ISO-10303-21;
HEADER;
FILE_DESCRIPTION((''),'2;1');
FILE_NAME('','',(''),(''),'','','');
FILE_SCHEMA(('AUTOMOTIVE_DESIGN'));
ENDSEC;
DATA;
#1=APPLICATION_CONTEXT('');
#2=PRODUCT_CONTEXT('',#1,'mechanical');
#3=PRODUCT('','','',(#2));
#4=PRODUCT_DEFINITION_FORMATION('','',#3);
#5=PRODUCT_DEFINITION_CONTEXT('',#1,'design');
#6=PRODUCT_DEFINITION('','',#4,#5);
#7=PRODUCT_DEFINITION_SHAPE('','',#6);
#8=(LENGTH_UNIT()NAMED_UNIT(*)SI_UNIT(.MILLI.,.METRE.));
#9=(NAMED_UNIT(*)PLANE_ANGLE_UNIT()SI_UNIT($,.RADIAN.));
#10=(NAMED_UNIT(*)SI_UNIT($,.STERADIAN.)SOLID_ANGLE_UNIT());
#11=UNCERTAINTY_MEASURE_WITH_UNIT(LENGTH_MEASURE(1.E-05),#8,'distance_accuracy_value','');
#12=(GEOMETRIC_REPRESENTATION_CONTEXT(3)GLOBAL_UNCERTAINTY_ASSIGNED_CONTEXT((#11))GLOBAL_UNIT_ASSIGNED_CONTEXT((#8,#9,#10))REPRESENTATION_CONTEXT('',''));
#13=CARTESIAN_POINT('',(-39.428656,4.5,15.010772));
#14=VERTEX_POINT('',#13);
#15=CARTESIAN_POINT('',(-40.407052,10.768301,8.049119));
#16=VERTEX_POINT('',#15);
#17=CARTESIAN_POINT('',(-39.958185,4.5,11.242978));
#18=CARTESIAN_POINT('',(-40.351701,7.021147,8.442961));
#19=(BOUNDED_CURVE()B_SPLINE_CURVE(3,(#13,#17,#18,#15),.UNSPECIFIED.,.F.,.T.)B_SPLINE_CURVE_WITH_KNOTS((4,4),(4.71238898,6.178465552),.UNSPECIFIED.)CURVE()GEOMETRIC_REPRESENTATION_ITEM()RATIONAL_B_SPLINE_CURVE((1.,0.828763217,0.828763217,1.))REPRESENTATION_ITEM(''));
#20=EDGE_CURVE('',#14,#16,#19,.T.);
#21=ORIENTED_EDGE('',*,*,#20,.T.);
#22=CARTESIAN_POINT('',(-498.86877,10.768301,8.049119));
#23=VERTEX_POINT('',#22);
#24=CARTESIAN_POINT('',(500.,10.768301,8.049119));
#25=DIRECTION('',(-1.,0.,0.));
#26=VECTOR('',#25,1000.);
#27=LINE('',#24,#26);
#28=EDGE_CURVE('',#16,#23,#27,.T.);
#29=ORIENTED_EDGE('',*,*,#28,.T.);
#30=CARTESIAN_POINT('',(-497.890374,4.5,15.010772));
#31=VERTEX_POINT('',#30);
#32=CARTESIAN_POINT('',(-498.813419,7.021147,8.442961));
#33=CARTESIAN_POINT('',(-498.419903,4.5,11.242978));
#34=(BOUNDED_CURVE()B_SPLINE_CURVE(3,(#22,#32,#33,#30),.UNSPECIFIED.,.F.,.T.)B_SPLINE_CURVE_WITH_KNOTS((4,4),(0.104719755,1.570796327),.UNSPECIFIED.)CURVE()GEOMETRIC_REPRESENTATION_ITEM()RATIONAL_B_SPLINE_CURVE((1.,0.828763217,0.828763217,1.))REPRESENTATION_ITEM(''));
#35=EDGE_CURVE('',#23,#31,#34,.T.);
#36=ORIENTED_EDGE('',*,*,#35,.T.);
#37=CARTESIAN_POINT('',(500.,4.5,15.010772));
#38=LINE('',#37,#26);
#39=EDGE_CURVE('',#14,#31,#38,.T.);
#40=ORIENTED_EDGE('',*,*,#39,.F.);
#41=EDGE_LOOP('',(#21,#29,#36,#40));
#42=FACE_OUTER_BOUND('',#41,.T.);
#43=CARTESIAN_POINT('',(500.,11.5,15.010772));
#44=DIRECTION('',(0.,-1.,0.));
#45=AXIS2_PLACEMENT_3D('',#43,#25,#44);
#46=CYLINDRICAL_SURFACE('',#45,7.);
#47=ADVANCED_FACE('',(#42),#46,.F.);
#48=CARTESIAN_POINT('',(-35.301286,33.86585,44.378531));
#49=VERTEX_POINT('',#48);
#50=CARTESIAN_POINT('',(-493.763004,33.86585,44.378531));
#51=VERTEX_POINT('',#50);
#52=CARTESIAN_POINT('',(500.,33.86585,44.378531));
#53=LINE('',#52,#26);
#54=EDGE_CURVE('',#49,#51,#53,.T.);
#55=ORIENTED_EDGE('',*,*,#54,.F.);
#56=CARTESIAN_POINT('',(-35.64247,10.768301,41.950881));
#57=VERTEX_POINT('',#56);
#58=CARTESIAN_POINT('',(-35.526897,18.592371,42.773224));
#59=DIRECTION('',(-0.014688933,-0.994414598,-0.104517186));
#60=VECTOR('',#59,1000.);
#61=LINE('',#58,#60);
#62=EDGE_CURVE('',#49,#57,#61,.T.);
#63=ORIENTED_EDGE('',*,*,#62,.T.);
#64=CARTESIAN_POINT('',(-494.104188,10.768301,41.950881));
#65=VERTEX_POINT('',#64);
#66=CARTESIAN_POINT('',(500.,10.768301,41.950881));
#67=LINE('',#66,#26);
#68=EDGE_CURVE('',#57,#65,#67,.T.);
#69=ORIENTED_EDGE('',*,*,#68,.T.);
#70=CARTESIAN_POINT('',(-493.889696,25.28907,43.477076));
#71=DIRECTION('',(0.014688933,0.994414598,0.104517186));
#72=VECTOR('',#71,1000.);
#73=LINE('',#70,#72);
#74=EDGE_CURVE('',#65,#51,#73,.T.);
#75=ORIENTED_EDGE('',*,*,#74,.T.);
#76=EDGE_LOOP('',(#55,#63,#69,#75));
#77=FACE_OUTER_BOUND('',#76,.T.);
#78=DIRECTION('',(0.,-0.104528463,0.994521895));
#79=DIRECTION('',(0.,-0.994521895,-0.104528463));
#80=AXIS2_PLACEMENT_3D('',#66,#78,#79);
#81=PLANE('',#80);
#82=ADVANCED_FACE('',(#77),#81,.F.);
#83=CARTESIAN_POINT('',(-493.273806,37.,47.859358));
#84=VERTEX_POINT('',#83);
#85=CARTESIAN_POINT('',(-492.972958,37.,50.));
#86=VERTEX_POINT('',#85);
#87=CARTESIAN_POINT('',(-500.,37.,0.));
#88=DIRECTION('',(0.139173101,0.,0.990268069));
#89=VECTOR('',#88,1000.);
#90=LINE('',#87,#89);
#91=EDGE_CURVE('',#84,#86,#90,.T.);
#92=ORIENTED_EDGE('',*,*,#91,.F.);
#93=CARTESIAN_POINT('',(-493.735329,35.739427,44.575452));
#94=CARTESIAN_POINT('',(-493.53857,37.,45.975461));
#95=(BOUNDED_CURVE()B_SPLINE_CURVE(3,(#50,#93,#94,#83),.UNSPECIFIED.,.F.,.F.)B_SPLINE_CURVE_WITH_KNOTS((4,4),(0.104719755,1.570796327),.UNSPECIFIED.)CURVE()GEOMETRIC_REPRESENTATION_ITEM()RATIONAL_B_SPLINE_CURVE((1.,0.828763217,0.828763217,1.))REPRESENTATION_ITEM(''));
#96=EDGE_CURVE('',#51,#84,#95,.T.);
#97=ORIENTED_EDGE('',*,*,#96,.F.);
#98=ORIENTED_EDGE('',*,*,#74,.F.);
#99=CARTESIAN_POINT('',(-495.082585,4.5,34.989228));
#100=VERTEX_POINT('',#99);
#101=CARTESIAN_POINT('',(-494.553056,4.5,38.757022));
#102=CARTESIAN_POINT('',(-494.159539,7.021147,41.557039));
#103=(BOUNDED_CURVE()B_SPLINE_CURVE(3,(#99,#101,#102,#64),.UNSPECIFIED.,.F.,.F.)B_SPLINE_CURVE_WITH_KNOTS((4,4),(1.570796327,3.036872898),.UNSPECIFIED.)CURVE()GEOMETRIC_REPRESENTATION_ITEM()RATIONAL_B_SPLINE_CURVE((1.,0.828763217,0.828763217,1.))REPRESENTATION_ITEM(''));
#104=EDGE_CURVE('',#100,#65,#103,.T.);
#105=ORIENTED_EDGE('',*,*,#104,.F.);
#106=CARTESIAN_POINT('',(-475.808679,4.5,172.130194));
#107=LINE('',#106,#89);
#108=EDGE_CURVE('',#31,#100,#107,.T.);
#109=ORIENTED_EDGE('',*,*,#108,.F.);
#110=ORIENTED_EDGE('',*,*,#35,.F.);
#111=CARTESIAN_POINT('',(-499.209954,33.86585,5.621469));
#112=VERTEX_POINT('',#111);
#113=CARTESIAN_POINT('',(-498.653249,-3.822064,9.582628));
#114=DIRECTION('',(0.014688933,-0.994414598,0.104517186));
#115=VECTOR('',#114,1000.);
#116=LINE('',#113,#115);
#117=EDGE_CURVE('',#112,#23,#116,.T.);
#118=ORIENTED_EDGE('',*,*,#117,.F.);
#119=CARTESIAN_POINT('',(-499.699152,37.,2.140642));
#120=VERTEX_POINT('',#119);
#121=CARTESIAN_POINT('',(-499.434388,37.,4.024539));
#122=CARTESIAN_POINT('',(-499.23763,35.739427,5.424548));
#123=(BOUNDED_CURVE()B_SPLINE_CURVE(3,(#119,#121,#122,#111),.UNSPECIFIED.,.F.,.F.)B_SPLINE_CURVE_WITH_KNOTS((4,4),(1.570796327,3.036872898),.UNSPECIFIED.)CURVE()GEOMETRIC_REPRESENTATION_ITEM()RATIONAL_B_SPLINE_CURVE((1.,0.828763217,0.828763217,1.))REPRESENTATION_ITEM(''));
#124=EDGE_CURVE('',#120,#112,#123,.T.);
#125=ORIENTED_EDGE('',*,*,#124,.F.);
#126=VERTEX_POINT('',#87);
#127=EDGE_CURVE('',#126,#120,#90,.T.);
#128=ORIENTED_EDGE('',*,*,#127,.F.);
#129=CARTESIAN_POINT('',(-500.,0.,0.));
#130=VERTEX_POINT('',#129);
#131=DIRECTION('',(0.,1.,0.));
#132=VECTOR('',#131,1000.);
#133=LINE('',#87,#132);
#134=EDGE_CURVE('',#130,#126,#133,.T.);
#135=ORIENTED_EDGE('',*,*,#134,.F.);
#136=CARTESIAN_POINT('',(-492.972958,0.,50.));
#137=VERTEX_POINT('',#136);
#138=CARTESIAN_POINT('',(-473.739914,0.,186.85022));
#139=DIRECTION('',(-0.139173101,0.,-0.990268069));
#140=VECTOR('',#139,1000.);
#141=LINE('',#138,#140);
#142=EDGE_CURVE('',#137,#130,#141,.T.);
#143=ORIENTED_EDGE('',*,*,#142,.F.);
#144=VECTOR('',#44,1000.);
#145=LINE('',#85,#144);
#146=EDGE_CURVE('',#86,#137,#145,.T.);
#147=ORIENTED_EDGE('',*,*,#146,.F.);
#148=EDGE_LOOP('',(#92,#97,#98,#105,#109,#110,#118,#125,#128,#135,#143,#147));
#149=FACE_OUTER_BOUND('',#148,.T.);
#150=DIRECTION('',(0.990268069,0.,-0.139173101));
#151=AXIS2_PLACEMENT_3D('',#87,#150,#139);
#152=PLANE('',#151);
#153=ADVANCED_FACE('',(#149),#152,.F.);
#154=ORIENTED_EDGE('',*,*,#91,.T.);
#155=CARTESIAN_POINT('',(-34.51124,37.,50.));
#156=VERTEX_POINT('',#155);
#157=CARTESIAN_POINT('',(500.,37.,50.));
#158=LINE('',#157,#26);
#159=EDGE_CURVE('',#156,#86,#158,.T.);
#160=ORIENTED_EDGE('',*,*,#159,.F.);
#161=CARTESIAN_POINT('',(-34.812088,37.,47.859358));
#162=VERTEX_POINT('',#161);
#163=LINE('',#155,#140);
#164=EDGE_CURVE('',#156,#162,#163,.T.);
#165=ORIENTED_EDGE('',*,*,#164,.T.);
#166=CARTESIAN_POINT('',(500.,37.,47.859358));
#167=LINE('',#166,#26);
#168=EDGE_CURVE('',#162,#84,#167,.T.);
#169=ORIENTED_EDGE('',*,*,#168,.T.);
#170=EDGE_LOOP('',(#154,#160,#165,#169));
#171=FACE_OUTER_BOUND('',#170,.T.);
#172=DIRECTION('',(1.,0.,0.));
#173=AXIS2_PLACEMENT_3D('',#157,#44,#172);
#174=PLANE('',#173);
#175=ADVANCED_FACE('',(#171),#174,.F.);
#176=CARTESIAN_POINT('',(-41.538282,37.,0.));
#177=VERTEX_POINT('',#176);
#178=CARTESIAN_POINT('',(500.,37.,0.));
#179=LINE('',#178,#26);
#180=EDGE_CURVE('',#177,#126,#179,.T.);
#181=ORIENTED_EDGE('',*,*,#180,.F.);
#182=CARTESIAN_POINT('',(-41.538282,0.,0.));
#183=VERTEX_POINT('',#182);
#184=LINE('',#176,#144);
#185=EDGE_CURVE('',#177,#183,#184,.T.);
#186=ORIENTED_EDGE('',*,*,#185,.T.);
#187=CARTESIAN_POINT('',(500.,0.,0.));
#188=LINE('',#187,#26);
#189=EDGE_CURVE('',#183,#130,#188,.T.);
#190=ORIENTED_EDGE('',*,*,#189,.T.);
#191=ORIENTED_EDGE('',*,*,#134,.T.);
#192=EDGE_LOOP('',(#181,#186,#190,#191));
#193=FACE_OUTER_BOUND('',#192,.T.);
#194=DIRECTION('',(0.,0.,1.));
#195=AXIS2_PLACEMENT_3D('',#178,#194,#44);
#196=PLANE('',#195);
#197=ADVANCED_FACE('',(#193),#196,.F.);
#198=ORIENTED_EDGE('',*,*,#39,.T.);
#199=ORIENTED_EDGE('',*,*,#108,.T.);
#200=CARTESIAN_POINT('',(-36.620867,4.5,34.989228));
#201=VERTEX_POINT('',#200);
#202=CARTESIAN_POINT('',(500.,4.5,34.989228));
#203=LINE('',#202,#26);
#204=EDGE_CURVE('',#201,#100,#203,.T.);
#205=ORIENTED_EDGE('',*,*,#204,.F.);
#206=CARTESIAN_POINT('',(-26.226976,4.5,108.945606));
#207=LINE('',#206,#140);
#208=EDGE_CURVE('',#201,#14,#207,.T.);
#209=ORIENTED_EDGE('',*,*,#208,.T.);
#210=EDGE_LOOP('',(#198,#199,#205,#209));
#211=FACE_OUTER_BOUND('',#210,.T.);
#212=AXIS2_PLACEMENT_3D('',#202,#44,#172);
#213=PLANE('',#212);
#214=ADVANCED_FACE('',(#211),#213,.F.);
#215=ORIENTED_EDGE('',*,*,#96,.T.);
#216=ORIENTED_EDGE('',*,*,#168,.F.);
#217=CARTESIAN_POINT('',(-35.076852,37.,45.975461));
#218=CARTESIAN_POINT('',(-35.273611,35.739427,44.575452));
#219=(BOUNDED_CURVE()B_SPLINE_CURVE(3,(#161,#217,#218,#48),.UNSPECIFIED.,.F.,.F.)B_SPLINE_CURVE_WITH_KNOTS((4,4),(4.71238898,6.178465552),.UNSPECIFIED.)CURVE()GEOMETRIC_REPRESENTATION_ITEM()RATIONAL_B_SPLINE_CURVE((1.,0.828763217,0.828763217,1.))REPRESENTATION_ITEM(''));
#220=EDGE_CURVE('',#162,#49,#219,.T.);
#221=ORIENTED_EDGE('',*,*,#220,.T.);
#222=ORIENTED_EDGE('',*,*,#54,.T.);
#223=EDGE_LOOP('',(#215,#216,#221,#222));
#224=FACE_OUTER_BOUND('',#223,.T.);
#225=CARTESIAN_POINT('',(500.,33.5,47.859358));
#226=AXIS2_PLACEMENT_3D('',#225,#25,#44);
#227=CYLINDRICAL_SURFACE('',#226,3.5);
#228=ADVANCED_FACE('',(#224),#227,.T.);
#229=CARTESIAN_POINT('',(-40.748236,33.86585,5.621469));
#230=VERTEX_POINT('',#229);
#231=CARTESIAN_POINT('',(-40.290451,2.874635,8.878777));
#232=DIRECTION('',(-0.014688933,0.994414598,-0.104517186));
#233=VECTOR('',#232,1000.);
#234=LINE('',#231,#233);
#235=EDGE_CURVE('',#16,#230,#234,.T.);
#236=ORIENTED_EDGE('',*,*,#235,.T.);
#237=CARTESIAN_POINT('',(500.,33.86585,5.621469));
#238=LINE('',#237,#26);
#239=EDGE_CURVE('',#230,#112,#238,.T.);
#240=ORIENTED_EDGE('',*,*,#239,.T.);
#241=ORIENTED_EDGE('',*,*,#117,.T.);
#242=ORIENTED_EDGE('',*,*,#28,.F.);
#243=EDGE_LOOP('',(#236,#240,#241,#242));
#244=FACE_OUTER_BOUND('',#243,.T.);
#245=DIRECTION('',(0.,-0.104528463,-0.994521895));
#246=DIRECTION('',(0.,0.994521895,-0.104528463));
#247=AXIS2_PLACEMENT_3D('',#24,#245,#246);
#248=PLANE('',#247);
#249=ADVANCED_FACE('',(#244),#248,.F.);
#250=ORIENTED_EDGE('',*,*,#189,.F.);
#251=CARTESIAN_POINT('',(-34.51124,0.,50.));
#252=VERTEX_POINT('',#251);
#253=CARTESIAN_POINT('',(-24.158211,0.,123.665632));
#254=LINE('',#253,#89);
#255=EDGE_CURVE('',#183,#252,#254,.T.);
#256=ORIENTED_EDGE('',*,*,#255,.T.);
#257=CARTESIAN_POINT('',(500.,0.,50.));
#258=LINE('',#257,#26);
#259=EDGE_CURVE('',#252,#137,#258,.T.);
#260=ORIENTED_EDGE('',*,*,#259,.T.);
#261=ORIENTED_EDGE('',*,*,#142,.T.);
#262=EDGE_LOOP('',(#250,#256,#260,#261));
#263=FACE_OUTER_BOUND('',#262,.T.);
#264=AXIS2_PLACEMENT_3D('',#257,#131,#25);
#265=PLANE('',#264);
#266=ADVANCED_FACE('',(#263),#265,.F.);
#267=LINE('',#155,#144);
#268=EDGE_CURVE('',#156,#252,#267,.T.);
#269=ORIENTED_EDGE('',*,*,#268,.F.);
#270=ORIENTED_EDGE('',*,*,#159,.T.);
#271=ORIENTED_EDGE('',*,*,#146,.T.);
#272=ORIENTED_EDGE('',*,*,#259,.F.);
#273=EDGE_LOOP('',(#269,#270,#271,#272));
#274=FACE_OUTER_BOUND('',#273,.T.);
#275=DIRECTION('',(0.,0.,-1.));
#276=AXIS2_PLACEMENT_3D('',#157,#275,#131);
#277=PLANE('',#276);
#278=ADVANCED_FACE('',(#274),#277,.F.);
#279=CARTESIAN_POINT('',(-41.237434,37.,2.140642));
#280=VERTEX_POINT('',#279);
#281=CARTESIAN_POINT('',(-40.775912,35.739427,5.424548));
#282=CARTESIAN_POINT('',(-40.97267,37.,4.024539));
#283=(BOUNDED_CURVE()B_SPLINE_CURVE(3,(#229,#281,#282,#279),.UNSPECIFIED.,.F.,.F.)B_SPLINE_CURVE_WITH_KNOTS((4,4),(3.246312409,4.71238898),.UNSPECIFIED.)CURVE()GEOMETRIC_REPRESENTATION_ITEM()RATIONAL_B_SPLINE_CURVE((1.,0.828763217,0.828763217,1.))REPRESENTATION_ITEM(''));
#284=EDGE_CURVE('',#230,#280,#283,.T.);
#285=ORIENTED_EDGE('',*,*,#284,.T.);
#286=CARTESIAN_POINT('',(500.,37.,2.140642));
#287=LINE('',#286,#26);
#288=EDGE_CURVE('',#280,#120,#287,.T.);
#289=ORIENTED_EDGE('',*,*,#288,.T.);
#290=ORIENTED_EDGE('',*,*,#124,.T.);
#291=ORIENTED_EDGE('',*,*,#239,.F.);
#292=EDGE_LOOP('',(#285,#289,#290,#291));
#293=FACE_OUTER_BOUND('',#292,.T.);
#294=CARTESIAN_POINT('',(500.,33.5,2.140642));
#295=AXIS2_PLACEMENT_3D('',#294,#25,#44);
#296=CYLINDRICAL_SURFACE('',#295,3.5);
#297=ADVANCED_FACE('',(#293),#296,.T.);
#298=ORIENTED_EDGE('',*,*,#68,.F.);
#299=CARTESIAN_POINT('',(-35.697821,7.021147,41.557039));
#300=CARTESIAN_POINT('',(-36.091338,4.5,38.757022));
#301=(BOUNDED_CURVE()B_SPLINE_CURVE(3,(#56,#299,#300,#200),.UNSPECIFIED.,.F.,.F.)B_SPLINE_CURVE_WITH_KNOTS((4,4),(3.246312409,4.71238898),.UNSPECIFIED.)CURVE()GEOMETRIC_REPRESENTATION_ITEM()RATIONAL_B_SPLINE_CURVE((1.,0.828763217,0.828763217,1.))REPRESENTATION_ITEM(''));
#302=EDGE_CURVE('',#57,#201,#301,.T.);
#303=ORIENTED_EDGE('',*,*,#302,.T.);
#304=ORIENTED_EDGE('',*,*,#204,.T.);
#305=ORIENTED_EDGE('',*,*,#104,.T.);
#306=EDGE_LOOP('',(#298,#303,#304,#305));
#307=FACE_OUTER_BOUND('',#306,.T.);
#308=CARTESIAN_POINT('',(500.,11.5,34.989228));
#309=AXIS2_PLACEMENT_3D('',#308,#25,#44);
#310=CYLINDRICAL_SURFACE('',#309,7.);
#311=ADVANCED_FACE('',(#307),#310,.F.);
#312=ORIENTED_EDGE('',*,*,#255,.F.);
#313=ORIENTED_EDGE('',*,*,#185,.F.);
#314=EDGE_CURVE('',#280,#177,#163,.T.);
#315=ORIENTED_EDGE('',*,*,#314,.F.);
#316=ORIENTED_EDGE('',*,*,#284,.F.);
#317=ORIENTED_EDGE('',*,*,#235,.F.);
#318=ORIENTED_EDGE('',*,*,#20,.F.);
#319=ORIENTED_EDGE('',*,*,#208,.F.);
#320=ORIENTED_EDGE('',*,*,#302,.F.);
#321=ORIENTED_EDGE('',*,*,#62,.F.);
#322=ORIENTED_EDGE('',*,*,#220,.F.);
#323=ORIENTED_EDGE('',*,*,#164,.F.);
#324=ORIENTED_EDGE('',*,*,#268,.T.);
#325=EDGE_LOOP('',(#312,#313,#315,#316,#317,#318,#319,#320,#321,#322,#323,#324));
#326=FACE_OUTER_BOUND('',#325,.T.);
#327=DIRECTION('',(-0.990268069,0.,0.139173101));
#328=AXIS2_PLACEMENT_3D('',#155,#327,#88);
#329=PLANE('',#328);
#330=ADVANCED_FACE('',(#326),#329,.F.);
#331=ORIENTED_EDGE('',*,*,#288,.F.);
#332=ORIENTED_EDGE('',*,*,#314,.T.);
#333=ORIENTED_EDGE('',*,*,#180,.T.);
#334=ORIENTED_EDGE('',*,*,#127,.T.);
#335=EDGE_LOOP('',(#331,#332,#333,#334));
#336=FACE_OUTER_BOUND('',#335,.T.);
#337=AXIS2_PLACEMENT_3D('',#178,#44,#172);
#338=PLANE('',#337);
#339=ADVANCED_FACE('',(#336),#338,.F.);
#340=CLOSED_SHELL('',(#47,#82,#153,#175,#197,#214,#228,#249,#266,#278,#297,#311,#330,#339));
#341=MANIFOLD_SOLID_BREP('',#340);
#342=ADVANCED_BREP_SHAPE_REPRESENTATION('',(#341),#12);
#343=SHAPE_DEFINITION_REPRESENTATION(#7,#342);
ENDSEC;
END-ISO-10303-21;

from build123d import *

# Parameters (mm, degrees)
GB_T_707_1988_HOT_ROLLED_CHANNEL_05_1_DEPTH = 1000
CUT_EXTRUDE6_DEPTH                          = 504.854145562
CUT_EXTRUDE6_DEPTH_BACK                     = 504.854145562


with BuildPart() as part:
    # Sketch1 → GB/T 707-1988 hot-rolled channel 05(1) (new body)
    with BuildSketch(Plane.YZ.offset(-500)):
        with BuildLine():
            Line((37, 50), (0, 50))
            Line((0, 50), (0, 0))
            Line((0, 0), (37, 0))
            Line((37, 0), (37, 2.140642022))
            ThreePointArc((37, 2.140642022), (36.101006889, 4.482599144), (33.865849621, 5.621468656))
            Line((33.865849621, 5.621468656), (10.768300757, 8.049118866))
            ThreePointArc((10.768300757, 8.049118866), (6.297986222, 10.326857889), (4.5, 15.010772133))
            Line((4.5, 15.010772133), (4.5, 34.989227867))
            ThreePointArc((4.5, 34.989227867), (6.297986222, 39.673142111), (10.768300757, 41.950881134))
            Line((10.768300757, 41.950881134), (33.865849621, 44.378531344))
            ThreePointArc((33.865849621, 44.378531344), (36.101006889, 45.517400856), (37, 47.859357978))
            Line((37, 47.859357978), (37, 50))
        make_face()
    extrude(amount=GB_T_707_1988_HOT_ROLLED_CHANNEL_05_1_DEPTH)

    # Sketch4 → Cut-Extrude6 (cut, two sides: drawn at the far end of the back side and taken through both)
    with BuildSketch(Plane.XZ.offset(-CUT_EXTRUDE6_DEPTH_BACK)):
        Polygon((-500, 50), (-500, 0), (-492.972958265, 50), align=None)
        Polygon((500, 50), (-34.511240341, 50), (-41.538282077, 0), (500, 0), align=None)
    extrude(amount=CUT_EXTRUDE6_DEPTH + CUT_EXTRUDE6_DEPTH_BACK, mode=Mode.SUBTRACT)


solid = part.part
